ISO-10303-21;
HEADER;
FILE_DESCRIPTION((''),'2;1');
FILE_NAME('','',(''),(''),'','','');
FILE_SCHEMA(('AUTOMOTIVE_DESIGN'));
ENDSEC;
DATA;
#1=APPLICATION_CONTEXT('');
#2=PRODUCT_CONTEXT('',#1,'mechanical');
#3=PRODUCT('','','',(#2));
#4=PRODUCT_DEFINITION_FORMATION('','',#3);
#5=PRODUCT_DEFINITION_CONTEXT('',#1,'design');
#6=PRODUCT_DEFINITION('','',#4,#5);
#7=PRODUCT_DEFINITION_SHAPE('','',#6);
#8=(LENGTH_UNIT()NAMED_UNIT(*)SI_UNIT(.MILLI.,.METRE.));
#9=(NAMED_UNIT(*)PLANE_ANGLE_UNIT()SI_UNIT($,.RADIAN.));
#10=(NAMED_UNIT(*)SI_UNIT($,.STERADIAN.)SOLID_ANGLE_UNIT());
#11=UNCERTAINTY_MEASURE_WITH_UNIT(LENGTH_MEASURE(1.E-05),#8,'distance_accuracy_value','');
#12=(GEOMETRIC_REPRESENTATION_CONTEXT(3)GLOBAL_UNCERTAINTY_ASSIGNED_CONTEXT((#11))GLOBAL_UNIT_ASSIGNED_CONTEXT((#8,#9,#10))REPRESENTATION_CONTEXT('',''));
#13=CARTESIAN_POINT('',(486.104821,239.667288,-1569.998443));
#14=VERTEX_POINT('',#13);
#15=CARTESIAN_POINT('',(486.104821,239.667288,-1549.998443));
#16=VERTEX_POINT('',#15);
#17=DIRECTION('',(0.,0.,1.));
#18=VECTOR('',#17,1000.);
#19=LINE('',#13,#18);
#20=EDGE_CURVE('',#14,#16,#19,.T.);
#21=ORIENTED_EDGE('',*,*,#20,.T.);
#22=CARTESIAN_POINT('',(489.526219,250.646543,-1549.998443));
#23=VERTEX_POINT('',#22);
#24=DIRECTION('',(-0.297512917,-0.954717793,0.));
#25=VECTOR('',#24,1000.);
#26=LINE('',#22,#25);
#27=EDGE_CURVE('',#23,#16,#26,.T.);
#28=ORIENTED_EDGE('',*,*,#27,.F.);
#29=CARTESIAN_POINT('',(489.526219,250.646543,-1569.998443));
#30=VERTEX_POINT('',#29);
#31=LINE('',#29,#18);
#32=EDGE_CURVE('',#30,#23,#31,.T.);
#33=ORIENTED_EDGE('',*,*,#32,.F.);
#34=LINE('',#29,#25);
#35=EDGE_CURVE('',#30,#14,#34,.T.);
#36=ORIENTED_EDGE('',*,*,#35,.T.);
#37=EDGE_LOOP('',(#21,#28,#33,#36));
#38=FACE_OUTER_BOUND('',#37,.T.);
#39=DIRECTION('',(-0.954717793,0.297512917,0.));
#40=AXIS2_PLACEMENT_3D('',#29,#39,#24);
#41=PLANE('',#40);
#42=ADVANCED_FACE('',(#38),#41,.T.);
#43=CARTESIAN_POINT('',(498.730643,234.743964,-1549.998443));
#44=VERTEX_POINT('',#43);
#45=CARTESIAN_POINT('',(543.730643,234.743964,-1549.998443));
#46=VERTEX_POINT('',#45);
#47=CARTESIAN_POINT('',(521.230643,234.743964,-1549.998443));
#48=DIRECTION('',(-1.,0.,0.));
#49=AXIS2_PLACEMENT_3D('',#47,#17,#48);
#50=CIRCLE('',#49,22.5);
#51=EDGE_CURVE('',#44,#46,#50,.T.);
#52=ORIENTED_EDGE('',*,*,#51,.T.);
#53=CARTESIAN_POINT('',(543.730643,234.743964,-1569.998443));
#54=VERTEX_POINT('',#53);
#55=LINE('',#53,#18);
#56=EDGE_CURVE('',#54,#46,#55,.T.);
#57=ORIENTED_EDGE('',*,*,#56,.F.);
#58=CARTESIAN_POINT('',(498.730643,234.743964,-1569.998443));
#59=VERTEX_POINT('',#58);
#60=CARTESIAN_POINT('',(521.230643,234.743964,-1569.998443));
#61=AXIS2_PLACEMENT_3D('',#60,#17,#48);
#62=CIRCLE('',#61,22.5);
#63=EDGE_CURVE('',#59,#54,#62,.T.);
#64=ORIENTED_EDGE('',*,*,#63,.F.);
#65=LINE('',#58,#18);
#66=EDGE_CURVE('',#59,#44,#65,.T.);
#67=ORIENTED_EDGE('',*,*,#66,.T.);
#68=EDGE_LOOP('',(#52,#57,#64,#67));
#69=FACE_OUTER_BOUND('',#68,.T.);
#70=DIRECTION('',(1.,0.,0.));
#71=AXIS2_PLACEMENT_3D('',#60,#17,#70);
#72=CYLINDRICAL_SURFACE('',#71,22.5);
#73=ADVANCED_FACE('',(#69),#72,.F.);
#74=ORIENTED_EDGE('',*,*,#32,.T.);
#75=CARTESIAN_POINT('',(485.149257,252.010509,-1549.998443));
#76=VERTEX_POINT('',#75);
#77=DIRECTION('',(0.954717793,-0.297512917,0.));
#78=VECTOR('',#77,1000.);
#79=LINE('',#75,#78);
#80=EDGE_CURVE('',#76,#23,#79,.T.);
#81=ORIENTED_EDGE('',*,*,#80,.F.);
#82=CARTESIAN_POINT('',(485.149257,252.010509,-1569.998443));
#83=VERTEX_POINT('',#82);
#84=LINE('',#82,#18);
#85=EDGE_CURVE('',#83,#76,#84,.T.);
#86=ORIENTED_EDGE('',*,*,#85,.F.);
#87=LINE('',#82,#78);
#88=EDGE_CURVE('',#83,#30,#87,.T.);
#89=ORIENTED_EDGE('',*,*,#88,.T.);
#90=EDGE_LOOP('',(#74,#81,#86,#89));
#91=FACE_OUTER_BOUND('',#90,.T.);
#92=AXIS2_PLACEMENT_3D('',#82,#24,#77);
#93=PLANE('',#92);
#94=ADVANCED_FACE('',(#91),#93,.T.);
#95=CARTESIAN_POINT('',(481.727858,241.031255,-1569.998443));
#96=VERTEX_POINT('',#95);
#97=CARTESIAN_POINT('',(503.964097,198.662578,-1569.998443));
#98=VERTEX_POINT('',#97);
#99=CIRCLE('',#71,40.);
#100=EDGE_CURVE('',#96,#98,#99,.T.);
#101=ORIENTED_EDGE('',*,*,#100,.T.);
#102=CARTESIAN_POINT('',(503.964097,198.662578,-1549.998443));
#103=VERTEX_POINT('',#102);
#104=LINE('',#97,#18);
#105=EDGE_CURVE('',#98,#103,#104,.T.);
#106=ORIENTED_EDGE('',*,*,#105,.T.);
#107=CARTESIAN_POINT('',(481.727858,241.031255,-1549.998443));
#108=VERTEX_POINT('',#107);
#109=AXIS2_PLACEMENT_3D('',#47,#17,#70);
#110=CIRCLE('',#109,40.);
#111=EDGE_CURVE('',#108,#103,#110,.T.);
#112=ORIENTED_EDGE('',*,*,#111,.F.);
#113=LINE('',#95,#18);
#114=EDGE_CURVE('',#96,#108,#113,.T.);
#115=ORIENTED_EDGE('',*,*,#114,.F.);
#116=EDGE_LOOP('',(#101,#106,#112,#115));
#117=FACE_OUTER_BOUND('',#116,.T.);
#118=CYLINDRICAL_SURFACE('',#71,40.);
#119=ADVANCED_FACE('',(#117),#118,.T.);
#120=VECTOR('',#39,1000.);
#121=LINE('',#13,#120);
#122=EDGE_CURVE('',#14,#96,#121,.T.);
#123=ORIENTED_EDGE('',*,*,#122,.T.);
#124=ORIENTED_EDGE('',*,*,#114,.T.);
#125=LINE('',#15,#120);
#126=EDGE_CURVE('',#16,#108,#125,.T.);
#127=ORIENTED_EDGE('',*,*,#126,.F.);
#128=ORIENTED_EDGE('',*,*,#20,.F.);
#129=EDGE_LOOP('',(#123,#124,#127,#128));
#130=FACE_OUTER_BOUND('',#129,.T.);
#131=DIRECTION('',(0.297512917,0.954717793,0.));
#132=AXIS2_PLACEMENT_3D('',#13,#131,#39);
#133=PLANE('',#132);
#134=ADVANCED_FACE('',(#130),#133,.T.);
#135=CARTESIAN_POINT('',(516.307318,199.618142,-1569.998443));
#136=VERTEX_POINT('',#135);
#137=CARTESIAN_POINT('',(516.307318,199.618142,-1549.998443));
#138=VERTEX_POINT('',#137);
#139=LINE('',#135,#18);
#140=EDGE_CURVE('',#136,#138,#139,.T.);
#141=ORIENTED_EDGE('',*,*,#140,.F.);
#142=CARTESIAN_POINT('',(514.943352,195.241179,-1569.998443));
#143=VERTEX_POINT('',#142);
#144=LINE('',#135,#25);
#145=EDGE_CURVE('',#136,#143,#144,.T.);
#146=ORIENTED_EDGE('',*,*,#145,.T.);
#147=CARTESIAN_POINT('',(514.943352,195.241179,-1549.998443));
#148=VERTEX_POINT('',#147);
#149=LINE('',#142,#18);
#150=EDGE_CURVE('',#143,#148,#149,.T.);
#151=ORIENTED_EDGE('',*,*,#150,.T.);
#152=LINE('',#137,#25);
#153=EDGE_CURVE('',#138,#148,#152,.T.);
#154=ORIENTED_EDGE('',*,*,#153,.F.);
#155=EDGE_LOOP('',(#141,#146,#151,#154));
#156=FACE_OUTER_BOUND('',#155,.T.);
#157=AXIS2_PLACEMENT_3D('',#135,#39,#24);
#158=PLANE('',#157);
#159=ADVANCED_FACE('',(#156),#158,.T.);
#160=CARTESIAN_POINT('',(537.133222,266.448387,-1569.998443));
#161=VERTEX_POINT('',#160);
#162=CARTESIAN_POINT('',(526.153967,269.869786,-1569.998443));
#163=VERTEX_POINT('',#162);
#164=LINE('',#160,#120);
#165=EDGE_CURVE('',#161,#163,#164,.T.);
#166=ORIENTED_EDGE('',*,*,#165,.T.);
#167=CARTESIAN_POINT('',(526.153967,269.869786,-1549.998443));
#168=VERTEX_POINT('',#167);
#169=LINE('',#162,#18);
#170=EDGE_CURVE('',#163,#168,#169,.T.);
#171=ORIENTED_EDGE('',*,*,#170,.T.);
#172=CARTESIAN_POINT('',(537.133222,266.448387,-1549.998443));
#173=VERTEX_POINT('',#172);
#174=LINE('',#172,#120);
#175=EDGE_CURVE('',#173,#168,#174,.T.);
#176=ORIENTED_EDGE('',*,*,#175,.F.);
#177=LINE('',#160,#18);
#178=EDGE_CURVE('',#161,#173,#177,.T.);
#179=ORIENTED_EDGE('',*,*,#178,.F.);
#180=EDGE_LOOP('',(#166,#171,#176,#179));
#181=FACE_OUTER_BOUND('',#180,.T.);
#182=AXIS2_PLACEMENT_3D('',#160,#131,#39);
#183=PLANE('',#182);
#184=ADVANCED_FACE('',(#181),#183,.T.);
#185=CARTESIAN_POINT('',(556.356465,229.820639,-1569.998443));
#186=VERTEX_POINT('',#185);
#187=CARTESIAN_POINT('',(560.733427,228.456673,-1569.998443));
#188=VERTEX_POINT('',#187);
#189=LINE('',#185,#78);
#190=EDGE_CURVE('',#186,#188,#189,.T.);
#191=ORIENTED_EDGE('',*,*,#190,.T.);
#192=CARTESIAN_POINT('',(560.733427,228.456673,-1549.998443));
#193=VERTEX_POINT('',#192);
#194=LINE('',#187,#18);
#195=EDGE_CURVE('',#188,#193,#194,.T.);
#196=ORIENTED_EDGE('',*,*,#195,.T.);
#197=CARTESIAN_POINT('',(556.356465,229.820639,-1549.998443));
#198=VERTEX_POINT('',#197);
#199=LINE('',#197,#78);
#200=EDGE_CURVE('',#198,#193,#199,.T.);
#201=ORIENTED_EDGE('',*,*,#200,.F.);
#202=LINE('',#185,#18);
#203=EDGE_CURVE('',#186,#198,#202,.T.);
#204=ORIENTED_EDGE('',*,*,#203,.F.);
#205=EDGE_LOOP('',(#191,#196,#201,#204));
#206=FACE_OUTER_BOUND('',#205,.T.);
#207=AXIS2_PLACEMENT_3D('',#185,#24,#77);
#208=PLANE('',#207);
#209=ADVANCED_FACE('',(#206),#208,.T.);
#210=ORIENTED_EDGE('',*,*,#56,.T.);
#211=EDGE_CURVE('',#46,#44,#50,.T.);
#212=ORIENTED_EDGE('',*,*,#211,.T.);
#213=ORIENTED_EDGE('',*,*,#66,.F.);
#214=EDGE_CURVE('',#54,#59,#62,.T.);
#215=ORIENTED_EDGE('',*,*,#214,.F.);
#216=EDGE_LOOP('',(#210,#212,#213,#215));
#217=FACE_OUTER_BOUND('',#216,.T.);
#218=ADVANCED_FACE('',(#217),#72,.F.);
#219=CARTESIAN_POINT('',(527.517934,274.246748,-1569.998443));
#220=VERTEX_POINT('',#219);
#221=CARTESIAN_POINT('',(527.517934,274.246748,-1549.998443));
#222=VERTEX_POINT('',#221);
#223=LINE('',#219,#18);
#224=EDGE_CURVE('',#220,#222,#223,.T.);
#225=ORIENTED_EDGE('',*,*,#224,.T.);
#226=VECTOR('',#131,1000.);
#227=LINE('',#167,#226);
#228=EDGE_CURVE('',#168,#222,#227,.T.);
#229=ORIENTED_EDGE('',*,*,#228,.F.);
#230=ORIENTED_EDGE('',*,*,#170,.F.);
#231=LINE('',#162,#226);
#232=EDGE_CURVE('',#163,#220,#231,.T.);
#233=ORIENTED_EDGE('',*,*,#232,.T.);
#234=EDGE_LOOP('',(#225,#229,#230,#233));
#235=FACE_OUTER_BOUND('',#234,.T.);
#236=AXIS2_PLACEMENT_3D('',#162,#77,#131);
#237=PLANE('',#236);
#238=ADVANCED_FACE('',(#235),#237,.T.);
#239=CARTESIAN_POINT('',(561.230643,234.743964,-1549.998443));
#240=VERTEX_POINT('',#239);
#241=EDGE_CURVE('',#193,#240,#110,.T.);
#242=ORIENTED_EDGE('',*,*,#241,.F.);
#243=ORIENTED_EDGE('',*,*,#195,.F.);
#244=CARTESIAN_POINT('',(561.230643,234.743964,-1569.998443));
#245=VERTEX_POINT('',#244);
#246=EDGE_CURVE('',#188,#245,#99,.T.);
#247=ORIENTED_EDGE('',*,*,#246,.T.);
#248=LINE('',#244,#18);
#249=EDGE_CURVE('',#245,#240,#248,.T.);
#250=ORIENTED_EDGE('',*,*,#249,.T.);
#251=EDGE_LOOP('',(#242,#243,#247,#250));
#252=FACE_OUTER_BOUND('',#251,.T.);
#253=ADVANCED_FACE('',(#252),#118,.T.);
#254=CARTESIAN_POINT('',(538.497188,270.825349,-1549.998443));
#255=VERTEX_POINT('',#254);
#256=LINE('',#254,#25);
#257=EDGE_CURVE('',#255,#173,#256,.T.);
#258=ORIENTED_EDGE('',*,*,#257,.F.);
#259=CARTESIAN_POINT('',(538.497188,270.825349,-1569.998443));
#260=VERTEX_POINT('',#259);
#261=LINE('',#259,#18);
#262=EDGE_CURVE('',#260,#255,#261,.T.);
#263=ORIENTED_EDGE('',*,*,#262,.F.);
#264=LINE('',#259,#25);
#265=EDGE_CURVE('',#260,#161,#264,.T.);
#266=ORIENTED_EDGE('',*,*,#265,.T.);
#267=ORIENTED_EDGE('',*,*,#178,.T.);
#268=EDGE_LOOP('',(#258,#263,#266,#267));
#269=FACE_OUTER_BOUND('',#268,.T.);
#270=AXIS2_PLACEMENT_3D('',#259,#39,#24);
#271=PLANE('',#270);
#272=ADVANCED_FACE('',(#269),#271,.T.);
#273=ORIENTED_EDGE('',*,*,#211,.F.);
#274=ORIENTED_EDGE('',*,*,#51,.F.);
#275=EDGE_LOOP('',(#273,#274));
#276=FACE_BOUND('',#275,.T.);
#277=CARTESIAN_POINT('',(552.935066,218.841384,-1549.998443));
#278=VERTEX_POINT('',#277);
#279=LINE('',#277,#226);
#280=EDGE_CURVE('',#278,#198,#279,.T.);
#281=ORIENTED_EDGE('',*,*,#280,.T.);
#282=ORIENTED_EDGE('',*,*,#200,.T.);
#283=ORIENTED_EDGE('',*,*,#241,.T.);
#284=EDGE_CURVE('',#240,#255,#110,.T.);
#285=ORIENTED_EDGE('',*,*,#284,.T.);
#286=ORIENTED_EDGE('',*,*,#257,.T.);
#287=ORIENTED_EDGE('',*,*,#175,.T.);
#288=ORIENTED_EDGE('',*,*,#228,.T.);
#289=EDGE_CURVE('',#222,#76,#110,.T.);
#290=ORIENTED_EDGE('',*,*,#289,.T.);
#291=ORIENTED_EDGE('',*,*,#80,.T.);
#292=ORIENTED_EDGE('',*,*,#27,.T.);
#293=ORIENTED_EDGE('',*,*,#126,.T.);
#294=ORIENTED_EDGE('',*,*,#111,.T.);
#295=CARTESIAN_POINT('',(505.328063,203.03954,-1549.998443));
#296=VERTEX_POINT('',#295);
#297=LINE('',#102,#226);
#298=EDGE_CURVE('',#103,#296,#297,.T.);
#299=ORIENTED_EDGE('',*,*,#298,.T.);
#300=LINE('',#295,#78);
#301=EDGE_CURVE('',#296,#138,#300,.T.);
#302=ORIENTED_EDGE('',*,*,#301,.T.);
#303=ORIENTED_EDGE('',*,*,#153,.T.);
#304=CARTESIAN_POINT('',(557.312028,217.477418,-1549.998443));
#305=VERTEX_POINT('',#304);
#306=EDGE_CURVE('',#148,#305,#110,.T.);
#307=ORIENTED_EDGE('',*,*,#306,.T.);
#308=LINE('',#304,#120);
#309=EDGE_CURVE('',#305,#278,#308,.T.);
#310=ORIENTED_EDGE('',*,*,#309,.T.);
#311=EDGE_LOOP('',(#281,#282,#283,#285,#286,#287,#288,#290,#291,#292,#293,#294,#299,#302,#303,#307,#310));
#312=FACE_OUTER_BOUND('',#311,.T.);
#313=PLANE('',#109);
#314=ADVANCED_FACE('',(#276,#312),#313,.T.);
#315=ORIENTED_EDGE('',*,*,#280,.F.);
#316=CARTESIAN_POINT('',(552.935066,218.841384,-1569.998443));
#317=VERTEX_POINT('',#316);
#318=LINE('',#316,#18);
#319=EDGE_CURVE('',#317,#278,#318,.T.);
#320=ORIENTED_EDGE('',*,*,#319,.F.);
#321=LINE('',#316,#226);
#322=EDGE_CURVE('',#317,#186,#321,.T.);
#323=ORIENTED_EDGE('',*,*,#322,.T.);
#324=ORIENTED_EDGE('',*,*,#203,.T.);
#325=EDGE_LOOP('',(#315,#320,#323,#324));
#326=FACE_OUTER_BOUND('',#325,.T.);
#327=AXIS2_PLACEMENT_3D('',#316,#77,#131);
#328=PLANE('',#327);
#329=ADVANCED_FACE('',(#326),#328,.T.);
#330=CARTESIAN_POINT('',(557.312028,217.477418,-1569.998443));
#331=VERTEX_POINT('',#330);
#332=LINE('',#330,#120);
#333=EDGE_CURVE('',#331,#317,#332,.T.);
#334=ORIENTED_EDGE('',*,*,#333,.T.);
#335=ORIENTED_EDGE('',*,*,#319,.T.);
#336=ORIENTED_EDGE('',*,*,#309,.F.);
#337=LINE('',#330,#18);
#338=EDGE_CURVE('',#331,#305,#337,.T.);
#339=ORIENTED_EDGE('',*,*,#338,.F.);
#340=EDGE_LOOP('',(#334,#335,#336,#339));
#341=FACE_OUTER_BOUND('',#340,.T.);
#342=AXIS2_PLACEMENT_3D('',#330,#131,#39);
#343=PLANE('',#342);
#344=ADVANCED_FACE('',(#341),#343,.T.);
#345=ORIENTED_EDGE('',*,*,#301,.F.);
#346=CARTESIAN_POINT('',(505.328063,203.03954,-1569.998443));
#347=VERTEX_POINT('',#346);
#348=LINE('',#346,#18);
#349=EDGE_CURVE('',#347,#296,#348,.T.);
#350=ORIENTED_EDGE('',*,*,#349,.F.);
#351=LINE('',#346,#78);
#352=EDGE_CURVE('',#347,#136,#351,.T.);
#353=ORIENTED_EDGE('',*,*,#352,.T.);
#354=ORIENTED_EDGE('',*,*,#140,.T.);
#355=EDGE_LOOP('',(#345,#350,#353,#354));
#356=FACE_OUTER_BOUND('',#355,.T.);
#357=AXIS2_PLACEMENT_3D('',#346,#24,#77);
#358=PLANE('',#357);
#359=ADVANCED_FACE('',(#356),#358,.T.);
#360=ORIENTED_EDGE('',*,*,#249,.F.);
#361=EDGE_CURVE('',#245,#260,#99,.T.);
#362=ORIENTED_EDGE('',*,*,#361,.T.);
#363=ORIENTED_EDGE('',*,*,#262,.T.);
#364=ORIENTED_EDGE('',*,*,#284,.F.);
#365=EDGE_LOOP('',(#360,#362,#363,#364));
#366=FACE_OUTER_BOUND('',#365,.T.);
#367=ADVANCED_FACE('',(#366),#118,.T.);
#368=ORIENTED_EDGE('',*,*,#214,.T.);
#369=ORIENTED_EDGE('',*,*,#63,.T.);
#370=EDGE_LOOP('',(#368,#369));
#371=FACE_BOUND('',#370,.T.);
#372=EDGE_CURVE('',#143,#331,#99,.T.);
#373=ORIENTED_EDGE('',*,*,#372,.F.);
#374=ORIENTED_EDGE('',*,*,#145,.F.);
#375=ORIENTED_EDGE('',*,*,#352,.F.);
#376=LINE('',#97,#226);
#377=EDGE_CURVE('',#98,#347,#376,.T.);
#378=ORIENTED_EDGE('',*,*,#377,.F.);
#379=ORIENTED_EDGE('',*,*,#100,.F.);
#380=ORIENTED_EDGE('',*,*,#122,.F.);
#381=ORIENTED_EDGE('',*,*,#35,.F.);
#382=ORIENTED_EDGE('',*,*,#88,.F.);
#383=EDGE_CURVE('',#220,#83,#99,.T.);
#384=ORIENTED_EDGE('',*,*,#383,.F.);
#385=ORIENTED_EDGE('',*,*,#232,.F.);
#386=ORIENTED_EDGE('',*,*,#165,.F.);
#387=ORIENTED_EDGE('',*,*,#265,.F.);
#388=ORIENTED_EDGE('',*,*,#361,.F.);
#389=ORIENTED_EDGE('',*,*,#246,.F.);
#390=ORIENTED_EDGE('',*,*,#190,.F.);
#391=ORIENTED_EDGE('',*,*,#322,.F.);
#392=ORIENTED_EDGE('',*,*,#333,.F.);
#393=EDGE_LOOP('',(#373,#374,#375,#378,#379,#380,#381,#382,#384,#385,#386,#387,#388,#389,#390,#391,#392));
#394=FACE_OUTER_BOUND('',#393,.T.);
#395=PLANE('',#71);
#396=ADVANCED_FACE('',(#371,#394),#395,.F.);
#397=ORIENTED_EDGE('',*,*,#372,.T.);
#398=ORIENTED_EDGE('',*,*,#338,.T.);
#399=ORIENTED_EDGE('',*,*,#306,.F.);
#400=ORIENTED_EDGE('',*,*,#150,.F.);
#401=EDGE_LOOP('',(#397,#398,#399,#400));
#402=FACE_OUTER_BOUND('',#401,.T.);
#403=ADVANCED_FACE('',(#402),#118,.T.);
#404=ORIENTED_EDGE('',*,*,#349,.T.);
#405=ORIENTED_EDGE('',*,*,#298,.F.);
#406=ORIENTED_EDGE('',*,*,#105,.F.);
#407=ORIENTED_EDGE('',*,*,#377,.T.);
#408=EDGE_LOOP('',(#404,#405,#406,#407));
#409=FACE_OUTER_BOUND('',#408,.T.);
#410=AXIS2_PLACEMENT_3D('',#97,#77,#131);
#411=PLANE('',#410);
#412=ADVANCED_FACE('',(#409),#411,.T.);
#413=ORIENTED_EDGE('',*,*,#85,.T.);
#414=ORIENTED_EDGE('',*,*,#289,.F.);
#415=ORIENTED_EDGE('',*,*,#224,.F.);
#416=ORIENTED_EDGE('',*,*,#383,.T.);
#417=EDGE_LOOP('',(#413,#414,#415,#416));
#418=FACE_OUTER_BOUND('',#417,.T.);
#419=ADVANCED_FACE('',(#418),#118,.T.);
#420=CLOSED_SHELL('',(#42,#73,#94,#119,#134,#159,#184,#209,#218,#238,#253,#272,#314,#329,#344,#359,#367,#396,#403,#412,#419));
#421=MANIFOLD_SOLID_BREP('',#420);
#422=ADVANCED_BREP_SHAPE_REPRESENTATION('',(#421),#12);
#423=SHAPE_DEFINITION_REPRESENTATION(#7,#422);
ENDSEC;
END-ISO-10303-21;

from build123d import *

# Parameters (mm, degrees)
SKETCH1_R           = 22.5
BOSS_EXTRUDE1_DEPTH = 20


with BuildPart() as part:
    # Sketch1 → Boss-Extrude1 (new body)
    with BuildSketch(Plane.XY.offset(-1549.998443067)):
        with BuildLine():
            Line((526.153967379, 269.86978568), (527.517933611, 274.246748006))
            ThreePointArc((527.517933611, 274.246748006), (502.642081617, 270.162396725), (485.149256781, 252.010509299))
            Line((485.149256781, 252.010509299), (489.526219107, 250.646543068))
            Line((489.526219107, 250.646543068), (486.104820559, 239.667288449))
            Line((486.104820559, 239.667288449), (481.727858233, 241.031254681))
            ThreePointArc((481.727858233, 241.031254681), (485.812209514, 216.155402687), (503.964096939, 198.662577851))
            Line((503.964096939, 198.662577851), (505.328063171, 203.039540177))
            Line((505.328063171, 203.039540177), (516.307317789, 199.618141629))
            Line((516.307317789, 199.618141629), (514.943351558, 195.241179303))
            ThreePointArc((514.943351558, 195.241179303), (539.819203552, 199.325530584), (557.312028388, 217.47741801))
            Line((557.312028388, 217.47741801), (552.935066061, 218.841384241))
            Line((552.935066061, 218.841384241), (556.35646461, 229.82063886))
            Line((556.35646461, 229.82063886), (560.733426936, 228.456672628))
            ThreePointArc((560.733426936, 228.456672628), (556.649075655, 253.332524622), (538.497188229, 270.825349458))
            Line((538.497188229, 270.825349458), (537.133221997, 266.448387132))
            Line((537.133221997, 266.448387132), (526.153967379, 269.86978568))
        make_face()
        with Locations(Location((521.230642584, 234.743963655, 0), (0, 0, 180))):
            Circle(SKETCH1_R, mode=Mode.SUBTRACT)
    extrude(amount=-BOSS_EXTRUDE1_DEPTH)


solid = part.part
